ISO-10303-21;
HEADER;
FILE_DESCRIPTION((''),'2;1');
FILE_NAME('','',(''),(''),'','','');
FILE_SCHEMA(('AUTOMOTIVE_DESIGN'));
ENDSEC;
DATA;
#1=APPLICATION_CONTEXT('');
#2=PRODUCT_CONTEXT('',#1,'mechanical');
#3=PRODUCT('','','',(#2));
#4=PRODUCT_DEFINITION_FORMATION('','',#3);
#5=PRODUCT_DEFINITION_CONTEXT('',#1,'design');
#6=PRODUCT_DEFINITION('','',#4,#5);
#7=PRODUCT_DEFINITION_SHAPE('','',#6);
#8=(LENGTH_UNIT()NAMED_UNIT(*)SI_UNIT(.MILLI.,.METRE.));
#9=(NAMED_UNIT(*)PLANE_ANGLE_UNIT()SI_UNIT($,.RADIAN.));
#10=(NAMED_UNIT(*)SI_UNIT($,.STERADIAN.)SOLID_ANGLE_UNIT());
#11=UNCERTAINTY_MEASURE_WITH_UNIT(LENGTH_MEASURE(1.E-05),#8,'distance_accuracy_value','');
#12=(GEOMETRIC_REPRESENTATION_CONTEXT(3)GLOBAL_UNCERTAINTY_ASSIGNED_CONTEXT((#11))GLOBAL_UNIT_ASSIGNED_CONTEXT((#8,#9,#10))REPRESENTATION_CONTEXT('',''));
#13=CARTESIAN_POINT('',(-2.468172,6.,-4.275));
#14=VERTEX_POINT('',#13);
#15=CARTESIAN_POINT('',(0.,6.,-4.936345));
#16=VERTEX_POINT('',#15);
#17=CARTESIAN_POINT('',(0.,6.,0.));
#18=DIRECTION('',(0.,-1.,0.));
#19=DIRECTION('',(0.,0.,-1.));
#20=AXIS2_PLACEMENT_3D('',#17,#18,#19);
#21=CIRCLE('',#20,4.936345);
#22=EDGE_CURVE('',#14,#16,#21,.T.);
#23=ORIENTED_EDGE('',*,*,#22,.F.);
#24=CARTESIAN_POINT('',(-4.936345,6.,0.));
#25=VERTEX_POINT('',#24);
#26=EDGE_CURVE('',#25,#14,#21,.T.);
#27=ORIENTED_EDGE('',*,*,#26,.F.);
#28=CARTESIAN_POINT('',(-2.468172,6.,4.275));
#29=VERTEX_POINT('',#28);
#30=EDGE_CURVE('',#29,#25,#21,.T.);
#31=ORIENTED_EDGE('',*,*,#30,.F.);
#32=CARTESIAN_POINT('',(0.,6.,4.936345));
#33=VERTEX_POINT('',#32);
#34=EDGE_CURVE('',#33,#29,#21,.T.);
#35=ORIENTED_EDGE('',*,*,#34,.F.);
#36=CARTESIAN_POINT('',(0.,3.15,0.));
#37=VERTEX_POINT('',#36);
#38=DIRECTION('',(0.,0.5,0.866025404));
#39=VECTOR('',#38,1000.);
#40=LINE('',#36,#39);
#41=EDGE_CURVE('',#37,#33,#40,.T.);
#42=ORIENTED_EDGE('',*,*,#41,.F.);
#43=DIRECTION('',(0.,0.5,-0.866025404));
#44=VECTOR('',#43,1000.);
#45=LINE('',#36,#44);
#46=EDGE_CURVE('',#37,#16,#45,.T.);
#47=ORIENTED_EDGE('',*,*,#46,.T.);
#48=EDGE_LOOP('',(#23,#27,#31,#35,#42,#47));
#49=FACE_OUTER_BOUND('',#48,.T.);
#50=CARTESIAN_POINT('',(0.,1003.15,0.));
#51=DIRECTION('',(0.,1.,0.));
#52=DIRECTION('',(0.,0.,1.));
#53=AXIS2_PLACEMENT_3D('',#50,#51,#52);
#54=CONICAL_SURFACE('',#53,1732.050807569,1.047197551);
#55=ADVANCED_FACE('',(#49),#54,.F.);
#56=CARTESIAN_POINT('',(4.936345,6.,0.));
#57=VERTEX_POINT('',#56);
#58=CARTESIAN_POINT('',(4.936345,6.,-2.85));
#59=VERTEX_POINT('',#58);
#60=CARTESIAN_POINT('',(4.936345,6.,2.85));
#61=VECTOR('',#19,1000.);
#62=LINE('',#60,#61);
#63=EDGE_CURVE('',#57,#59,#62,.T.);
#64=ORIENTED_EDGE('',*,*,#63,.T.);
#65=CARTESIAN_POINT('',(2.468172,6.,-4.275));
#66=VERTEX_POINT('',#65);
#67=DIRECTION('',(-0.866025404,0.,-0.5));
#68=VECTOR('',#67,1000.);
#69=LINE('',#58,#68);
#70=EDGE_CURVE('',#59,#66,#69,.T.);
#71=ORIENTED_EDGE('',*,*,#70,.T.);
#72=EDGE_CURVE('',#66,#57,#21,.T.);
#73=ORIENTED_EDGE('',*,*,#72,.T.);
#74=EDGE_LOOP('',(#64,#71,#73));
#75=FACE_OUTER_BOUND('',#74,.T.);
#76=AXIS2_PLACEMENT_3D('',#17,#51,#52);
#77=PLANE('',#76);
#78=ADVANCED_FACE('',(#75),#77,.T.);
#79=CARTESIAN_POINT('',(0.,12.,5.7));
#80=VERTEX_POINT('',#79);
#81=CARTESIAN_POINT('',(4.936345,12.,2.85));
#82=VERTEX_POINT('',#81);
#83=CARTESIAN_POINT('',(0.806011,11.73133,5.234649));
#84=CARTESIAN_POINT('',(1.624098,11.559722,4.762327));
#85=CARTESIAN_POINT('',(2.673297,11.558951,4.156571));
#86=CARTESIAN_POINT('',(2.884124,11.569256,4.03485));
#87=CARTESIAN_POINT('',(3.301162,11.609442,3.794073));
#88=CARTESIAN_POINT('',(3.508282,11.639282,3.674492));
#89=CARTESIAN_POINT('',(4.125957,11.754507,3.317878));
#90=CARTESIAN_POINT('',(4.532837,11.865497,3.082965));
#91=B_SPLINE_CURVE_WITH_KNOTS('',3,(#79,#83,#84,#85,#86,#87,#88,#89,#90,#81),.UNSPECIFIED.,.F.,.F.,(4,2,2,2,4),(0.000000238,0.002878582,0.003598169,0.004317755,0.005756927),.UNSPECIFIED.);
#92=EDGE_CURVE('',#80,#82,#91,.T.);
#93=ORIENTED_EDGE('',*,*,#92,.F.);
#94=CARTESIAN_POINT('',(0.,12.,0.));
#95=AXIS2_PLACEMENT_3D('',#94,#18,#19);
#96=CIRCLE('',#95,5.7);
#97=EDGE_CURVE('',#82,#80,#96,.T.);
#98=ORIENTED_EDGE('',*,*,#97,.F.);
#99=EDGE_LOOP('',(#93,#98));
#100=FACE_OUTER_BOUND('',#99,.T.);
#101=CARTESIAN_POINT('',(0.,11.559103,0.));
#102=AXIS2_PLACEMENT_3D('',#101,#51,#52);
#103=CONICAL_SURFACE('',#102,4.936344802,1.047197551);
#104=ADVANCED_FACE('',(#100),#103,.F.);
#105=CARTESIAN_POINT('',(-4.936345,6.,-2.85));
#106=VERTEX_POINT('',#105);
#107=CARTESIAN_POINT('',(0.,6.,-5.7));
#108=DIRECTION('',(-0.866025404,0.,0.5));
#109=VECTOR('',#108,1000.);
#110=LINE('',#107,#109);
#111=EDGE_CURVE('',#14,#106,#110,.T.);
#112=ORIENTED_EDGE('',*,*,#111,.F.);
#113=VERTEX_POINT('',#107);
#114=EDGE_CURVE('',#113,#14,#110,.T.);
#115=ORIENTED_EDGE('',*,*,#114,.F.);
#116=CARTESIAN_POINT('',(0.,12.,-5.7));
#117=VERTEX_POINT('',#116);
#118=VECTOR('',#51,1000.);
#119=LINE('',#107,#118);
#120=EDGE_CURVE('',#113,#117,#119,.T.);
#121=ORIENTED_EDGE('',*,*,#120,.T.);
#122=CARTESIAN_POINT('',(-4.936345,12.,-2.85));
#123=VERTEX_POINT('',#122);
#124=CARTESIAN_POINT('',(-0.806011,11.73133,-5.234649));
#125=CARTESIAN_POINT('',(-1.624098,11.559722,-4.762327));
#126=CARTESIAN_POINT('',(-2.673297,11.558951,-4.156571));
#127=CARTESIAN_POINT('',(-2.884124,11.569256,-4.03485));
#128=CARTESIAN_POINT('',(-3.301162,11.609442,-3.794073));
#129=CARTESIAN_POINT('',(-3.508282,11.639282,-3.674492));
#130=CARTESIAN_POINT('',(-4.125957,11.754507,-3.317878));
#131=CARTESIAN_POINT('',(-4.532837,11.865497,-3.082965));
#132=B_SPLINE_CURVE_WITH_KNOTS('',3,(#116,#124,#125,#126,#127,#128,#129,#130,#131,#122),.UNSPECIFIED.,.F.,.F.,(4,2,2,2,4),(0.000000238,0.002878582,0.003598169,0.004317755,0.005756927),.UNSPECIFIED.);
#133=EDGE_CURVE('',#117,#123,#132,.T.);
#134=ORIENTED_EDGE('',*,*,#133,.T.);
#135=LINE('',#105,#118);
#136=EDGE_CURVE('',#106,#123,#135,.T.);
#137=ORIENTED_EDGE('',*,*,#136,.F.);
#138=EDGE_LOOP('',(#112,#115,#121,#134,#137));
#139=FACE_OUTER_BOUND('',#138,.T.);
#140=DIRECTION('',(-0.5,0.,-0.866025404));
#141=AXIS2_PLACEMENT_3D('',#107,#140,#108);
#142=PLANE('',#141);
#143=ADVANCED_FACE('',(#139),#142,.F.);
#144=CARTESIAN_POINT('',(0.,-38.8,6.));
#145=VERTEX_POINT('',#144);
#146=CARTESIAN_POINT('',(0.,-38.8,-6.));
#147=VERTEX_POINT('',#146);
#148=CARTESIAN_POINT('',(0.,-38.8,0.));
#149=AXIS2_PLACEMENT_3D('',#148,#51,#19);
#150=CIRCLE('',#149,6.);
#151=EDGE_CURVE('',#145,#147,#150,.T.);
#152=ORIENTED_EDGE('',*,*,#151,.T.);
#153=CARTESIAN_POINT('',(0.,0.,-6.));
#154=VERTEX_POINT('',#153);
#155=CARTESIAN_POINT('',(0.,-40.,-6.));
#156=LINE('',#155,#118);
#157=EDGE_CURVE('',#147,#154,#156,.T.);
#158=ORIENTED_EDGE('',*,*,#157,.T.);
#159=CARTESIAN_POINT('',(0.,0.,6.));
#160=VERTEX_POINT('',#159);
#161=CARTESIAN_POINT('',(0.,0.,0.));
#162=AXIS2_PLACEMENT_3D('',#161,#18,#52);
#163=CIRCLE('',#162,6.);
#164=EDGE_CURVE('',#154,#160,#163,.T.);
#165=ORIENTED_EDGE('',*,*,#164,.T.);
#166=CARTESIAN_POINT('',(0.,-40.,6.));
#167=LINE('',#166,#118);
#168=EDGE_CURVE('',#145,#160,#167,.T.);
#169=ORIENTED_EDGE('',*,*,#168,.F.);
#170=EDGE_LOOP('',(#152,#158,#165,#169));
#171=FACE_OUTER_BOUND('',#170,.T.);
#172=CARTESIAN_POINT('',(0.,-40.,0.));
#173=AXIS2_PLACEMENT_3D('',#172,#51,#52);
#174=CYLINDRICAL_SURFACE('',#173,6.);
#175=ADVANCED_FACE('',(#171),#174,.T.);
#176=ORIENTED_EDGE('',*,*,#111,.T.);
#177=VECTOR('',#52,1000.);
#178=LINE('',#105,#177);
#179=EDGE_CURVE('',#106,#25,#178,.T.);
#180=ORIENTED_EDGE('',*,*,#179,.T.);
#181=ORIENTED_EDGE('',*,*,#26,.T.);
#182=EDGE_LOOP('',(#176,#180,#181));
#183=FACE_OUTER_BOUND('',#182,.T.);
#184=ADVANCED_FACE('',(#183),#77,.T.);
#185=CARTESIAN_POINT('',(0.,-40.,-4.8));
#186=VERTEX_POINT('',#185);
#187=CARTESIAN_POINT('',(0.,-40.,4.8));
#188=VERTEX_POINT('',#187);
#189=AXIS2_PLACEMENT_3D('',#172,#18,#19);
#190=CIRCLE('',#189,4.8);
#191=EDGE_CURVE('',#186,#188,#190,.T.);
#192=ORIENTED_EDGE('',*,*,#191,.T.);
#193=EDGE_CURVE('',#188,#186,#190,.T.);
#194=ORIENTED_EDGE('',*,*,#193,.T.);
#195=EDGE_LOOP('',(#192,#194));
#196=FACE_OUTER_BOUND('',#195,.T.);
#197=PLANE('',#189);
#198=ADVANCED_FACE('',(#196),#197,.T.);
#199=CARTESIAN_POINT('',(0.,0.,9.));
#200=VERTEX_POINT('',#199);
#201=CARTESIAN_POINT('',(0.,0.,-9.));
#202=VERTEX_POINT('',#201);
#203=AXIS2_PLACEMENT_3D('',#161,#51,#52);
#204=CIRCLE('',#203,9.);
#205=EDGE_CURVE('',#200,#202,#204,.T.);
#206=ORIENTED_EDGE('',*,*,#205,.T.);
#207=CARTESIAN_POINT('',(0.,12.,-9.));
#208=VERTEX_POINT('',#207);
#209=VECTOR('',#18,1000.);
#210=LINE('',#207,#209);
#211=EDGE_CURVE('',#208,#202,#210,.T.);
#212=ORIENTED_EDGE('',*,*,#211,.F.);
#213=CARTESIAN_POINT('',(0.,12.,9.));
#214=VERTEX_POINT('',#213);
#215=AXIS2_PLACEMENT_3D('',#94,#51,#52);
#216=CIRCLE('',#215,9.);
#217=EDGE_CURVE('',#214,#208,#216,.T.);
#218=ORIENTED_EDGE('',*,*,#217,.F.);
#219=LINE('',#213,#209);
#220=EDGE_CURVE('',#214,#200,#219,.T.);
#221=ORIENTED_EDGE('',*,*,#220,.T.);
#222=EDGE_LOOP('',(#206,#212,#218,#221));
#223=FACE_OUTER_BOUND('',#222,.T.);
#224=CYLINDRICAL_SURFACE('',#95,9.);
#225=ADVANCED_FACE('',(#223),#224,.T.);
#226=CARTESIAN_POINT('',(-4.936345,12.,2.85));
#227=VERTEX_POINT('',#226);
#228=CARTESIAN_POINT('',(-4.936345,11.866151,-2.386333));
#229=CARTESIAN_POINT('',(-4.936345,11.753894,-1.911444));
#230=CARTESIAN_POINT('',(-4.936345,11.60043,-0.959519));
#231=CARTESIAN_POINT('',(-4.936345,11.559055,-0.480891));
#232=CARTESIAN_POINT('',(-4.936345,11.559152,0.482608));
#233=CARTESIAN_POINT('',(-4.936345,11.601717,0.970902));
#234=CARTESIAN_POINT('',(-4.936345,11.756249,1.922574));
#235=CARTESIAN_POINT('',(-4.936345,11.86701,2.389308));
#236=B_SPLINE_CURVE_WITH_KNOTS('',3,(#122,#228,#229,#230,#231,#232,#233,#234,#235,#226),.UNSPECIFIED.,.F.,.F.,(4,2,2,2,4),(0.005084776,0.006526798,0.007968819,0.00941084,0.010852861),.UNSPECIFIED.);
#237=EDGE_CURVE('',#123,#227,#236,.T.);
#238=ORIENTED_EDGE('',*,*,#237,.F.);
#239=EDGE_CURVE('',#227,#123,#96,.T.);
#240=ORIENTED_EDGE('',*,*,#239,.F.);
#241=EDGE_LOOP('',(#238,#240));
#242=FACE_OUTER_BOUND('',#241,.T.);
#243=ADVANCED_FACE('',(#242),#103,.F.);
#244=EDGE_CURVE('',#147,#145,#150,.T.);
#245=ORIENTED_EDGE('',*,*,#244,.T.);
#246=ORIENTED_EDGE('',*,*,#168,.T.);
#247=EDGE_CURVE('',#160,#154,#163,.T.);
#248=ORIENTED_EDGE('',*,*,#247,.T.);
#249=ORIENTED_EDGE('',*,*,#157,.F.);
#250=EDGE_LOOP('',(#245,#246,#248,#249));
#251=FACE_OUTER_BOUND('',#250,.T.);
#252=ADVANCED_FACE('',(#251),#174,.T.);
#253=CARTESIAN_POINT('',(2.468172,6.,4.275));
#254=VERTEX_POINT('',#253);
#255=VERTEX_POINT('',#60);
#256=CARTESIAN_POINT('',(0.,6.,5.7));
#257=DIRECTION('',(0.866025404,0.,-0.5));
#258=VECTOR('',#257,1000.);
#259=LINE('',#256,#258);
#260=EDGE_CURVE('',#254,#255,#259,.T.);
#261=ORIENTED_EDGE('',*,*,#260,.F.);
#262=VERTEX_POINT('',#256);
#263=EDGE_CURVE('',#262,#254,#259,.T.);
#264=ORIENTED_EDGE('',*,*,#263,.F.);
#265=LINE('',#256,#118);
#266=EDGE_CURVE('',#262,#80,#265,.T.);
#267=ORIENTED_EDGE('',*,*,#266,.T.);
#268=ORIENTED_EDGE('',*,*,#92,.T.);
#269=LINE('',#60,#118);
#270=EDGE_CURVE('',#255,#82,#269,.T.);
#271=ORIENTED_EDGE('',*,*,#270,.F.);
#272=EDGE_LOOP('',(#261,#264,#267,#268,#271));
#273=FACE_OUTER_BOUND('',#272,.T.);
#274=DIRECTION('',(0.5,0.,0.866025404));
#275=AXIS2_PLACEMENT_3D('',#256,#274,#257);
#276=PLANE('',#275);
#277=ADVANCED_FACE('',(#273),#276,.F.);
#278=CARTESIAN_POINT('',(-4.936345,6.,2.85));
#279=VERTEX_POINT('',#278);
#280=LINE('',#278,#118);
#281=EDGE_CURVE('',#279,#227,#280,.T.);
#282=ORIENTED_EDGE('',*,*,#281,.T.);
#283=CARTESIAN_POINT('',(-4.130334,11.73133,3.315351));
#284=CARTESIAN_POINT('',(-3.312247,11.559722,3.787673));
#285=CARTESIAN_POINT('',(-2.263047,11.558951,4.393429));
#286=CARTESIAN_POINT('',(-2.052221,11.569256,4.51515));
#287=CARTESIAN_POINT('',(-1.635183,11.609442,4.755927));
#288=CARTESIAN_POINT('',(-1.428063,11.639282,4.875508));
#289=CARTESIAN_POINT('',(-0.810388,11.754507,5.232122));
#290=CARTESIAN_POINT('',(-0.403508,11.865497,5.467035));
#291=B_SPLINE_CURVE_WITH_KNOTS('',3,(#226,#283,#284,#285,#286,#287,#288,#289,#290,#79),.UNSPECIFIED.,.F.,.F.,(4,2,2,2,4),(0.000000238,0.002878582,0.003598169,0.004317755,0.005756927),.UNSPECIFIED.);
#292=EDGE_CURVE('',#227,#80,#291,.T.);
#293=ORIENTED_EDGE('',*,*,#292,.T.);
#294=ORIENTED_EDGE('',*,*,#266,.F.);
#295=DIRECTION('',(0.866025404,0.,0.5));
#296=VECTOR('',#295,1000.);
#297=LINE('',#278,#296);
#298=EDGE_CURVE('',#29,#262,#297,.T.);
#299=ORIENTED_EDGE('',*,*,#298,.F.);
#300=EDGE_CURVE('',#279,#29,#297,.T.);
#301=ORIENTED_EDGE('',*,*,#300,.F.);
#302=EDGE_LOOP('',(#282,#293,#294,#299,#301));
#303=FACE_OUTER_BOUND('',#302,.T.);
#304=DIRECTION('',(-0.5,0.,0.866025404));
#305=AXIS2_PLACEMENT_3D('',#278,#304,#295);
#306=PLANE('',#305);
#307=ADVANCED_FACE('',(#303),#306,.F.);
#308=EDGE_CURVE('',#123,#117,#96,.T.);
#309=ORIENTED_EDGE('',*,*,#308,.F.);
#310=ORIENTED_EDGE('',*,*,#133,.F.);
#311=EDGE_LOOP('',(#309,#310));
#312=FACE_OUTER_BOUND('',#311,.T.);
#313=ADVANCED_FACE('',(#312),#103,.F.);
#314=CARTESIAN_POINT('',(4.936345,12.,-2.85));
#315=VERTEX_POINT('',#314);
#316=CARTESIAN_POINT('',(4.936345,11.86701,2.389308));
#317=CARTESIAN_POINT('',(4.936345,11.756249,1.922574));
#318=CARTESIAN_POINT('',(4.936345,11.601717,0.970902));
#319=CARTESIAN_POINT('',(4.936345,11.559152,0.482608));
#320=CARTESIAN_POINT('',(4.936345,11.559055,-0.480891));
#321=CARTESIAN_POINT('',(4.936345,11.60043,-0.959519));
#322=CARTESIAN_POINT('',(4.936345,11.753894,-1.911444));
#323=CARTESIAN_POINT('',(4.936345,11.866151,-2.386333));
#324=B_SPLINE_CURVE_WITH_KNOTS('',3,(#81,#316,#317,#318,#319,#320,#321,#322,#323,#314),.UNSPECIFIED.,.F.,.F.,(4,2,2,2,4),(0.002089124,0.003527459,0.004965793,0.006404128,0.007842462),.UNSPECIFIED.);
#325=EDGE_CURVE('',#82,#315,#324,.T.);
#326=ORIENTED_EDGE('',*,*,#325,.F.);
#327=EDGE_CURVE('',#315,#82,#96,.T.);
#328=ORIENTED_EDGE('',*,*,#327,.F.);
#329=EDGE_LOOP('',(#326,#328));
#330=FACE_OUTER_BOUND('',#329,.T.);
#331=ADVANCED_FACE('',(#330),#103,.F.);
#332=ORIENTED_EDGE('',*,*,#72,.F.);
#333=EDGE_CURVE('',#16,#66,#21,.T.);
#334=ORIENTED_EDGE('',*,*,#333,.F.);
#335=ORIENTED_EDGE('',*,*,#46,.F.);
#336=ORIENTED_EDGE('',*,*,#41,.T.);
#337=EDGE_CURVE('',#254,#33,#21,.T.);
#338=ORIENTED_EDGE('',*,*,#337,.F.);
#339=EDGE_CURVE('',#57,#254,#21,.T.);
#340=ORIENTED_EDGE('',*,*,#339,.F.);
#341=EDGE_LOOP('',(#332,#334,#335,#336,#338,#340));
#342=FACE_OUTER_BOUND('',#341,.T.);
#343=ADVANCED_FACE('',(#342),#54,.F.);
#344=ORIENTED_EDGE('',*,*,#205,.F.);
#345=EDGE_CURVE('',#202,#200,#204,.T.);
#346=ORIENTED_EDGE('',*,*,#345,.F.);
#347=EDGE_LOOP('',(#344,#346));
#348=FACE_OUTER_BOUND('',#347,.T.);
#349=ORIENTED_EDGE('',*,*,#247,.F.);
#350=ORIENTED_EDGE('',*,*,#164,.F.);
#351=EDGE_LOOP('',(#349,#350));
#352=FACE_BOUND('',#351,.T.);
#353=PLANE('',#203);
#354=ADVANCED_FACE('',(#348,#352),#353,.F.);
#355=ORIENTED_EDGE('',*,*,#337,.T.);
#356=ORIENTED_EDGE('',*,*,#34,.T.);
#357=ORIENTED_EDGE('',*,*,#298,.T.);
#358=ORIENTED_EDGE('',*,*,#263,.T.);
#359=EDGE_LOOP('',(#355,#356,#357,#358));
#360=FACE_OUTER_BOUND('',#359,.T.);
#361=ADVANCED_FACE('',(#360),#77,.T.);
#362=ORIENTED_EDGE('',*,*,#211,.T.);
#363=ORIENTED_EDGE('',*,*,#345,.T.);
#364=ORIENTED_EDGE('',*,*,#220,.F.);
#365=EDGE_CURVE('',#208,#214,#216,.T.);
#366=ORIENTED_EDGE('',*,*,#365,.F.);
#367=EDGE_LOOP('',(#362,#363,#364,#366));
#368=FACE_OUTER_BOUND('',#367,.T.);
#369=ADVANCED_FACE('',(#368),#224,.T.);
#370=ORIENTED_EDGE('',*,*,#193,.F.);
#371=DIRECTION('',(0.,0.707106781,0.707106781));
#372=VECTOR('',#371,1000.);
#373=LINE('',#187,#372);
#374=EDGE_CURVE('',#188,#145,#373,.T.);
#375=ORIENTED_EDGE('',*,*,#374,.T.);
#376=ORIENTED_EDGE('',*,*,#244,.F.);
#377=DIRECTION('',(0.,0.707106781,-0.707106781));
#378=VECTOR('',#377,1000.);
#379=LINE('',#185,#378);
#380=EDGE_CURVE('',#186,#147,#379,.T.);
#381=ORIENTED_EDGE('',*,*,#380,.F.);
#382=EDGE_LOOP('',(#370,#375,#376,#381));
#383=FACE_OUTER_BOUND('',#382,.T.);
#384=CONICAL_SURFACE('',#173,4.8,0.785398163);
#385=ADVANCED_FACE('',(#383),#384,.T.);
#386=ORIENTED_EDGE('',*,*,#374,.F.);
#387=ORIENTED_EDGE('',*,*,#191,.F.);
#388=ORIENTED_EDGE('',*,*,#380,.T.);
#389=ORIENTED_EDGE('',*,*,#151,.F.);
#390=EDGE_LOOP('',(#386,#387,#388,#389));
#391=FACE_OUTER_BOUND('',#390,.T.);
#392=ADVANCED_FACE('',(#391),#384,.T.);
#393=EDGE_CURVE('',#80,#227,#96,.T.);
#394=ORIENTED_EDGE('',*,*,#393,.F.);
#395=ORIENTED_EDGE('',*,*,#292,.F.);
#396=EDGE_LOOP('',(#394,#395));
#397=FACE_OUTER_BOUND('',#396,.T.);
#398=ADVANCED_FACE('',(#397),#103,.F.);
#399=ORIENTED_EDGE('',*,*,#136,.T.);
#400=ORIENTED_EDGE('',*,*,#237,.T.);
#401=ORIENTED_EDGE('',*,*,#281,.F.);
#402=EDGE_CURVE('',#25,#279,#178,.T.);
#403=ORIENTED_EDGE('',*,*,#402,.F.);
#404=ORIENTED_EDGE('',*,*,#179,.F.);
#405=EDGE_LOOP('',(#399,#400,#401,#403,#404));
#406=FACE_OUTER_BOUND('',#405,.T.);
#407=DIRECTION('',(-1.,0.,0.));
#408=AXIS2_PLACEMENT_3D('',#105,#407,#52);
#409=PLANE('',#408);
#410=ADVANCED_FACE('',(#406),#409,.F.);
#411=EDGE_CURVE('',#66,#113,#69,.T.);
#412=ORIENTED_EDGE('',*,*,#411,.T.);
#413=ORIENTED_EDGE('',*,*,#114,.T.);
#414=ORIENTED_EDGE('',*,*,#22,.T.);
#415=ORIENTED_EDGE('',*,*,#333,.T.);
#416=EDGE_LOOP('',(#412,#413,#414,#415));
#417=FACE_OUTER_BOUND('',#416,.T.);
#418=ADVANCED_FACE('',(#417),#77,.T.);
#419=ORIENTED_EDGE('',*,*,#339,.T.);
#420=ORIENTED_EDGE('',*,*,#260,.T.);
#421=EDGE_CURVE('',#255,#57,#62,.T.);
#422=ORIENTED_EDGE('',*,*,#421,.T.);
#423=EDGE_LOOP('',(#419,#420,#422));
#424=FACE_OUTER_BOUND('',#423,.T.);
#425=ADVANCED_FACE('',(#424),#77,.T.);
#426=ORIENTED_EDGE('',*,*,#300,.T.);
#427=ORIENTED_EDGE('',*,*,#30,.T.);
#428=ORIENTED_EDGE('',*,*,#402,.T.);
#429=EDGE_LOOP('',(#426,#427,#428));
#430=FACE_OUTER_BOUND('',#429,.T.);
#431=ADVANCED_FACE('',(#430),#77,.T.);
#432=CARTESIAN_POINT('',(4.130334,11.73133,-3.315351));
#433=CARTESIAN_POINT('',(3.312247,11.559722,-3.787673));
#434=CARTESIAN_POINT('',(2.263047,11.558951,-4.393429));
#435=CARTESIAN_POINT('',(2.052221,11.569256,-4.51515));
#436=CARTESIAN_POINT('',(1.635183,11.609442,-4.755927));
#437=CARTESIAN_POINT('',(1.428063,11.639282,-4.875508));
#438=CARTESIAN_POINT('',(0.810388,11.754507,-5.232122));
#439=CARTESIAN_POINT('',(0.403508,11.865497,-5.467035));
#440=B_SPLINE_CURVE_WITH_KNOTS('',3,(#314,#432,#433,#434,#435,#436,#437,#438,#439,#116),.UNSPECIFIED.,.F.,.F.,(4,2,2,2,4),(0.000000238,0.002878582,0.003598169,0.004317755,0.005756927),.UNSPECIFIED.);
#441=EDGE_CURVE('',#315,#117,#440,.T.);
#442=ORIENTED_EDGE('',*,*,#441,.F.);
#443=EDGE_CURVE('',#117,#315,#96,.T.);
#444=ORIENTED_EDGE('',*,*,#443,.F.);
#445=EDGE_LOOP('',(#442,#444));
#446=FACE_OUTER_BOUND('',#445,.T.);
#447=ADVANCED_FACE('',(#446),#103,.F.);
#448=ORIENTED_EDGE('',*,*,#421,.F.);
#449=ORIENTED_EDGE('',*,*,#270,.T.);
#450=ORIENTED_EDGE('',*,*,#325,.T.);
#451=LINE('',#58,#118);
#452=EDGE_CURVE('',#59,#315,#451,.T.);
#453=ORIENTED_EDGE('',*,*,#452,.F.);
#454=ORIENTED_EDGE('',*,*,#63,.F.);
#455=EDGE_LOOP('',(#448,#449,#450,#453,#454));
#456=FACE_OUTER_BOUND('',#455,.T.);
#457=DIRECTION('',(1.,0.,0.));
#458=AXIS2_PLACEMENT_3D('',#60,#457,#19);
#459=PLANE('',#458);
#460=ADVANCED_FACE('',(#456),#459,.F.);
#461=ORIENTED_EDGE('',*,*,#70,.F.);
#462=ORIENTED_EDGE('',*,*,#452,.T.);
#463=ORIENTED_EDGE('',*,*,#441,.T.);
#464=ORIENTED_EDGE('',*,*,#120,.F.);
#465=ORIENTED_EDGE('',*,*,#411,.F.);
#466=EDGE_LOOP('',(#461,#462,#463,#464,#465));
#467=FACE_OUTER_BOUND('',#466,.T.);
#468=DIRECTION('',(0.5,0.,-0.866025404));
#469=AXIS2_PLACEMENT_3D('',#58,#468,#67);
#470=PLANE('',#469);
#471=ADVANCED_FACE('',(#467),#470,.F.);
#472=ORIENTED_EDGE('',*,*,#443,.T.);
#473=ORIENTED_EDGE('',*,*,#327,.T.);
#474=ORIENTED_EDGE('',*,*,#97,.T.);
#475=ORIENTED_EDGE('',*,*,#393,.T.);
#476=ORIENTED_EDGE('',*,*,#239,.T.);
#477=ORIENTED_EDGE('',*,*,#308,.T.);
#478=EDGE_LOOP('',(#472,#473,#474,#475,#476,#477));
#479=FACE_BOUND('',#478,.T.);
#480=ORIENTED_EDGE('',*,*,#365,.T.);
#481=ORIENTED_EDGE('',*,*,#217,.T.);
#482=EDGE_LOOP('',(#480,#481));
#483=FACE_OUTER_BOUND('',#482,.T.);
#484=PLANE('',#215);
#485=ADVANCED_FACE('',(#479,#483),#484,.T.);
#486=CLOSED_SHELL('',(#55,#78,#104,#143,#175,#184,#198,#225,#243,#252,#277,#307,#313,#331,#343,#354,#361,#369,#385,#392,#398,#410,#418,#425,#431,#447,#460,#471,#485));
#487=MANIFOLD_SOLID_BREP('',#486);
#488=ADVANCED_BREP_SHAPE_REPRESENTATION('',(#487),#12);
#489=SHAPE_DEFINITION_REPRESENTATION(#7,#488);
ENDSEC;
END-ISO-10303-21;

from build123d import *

# Parameters (mm, degrees)
SKETCH1_R           = 9
BOSS_EXTRUDE1_DEPTH = 12
SKETCH2_R           = 6
BOSS_EXTRUDE2_DEPTH = 40
CUT_EXTRUDE1_DEPTH  = 6
CHAMFER1_SIZE       = 1.2


with BuildPart() as part:
    # Sketch1 → Boss-Extrude1 (new body)
    with BuildSketch(Plane(origin=(0, 0, 0), x_dir=(1, 0, 0), z_dir=(0, 1, 0))):
        with Locations(Location((0, 0, 0), (0, 0, 270))):
            Circle(SKETCH1_R)
    extrude(amount=BOSS_EXTRUDE1_DEPTH)

    # Sketch2 → Boss-Extrude2 (add)
    with BuildSketch(Plane.XZ):
        with Locations(Location((0, 0, 0), (0, 0, 90))):
            Circle(SKETCH2_R)
    extrude(amount=BOSS_EXTRUDE2_DEPTH)

    # Sketch3 → Cut-Extrude1 (cut)
    with BuildSketch(Plane(origin=(0, 12, 0), x_dir=(1, 0, 0), z_dir=(0, 1, 0))):
        Polygon((0, 5.7), (-4.936344802, 2.85), (-4.936344802, -2.85), (0, -5.7), (4.936344802, -2.85), (4.936344802, 2.85), align=None)
    extrude(amount=-CUT_EXTRUDE1_DEPTH, mode=Mode.SUBTRACT)

    # Sketch4 → Cut-Revolve1 (revolve, cut)
    with BuildSketch(Plane.XY, mode=Mode.PRIVATE) as cut_revolve1_sk:
        Polygon((0, 6), (4.936344802, 6), (0, 3.15), align=None)
        Polygon((4.936344802, 11.559103466), (4.936344802, 12), (5.7, 12), align=None)
    revolve(cut_revolve1_sk.sketch.rotate(Axis((0, -3.932195077, 0), (0, 1, 0)), 270), axis=Axis((0, -3.932195077, 0), (0, 1, 0)), mode=Mode.SUBTRACT)

    # Chamfer1
    chamfer1_edges = [part.edges().sort_by_distance(p)[0] for p in [
        (0, -40, -6),
    ]]
    chamfer(chamfer1_edges, length=CHAMFER1_SIZE)


solid = part.part
